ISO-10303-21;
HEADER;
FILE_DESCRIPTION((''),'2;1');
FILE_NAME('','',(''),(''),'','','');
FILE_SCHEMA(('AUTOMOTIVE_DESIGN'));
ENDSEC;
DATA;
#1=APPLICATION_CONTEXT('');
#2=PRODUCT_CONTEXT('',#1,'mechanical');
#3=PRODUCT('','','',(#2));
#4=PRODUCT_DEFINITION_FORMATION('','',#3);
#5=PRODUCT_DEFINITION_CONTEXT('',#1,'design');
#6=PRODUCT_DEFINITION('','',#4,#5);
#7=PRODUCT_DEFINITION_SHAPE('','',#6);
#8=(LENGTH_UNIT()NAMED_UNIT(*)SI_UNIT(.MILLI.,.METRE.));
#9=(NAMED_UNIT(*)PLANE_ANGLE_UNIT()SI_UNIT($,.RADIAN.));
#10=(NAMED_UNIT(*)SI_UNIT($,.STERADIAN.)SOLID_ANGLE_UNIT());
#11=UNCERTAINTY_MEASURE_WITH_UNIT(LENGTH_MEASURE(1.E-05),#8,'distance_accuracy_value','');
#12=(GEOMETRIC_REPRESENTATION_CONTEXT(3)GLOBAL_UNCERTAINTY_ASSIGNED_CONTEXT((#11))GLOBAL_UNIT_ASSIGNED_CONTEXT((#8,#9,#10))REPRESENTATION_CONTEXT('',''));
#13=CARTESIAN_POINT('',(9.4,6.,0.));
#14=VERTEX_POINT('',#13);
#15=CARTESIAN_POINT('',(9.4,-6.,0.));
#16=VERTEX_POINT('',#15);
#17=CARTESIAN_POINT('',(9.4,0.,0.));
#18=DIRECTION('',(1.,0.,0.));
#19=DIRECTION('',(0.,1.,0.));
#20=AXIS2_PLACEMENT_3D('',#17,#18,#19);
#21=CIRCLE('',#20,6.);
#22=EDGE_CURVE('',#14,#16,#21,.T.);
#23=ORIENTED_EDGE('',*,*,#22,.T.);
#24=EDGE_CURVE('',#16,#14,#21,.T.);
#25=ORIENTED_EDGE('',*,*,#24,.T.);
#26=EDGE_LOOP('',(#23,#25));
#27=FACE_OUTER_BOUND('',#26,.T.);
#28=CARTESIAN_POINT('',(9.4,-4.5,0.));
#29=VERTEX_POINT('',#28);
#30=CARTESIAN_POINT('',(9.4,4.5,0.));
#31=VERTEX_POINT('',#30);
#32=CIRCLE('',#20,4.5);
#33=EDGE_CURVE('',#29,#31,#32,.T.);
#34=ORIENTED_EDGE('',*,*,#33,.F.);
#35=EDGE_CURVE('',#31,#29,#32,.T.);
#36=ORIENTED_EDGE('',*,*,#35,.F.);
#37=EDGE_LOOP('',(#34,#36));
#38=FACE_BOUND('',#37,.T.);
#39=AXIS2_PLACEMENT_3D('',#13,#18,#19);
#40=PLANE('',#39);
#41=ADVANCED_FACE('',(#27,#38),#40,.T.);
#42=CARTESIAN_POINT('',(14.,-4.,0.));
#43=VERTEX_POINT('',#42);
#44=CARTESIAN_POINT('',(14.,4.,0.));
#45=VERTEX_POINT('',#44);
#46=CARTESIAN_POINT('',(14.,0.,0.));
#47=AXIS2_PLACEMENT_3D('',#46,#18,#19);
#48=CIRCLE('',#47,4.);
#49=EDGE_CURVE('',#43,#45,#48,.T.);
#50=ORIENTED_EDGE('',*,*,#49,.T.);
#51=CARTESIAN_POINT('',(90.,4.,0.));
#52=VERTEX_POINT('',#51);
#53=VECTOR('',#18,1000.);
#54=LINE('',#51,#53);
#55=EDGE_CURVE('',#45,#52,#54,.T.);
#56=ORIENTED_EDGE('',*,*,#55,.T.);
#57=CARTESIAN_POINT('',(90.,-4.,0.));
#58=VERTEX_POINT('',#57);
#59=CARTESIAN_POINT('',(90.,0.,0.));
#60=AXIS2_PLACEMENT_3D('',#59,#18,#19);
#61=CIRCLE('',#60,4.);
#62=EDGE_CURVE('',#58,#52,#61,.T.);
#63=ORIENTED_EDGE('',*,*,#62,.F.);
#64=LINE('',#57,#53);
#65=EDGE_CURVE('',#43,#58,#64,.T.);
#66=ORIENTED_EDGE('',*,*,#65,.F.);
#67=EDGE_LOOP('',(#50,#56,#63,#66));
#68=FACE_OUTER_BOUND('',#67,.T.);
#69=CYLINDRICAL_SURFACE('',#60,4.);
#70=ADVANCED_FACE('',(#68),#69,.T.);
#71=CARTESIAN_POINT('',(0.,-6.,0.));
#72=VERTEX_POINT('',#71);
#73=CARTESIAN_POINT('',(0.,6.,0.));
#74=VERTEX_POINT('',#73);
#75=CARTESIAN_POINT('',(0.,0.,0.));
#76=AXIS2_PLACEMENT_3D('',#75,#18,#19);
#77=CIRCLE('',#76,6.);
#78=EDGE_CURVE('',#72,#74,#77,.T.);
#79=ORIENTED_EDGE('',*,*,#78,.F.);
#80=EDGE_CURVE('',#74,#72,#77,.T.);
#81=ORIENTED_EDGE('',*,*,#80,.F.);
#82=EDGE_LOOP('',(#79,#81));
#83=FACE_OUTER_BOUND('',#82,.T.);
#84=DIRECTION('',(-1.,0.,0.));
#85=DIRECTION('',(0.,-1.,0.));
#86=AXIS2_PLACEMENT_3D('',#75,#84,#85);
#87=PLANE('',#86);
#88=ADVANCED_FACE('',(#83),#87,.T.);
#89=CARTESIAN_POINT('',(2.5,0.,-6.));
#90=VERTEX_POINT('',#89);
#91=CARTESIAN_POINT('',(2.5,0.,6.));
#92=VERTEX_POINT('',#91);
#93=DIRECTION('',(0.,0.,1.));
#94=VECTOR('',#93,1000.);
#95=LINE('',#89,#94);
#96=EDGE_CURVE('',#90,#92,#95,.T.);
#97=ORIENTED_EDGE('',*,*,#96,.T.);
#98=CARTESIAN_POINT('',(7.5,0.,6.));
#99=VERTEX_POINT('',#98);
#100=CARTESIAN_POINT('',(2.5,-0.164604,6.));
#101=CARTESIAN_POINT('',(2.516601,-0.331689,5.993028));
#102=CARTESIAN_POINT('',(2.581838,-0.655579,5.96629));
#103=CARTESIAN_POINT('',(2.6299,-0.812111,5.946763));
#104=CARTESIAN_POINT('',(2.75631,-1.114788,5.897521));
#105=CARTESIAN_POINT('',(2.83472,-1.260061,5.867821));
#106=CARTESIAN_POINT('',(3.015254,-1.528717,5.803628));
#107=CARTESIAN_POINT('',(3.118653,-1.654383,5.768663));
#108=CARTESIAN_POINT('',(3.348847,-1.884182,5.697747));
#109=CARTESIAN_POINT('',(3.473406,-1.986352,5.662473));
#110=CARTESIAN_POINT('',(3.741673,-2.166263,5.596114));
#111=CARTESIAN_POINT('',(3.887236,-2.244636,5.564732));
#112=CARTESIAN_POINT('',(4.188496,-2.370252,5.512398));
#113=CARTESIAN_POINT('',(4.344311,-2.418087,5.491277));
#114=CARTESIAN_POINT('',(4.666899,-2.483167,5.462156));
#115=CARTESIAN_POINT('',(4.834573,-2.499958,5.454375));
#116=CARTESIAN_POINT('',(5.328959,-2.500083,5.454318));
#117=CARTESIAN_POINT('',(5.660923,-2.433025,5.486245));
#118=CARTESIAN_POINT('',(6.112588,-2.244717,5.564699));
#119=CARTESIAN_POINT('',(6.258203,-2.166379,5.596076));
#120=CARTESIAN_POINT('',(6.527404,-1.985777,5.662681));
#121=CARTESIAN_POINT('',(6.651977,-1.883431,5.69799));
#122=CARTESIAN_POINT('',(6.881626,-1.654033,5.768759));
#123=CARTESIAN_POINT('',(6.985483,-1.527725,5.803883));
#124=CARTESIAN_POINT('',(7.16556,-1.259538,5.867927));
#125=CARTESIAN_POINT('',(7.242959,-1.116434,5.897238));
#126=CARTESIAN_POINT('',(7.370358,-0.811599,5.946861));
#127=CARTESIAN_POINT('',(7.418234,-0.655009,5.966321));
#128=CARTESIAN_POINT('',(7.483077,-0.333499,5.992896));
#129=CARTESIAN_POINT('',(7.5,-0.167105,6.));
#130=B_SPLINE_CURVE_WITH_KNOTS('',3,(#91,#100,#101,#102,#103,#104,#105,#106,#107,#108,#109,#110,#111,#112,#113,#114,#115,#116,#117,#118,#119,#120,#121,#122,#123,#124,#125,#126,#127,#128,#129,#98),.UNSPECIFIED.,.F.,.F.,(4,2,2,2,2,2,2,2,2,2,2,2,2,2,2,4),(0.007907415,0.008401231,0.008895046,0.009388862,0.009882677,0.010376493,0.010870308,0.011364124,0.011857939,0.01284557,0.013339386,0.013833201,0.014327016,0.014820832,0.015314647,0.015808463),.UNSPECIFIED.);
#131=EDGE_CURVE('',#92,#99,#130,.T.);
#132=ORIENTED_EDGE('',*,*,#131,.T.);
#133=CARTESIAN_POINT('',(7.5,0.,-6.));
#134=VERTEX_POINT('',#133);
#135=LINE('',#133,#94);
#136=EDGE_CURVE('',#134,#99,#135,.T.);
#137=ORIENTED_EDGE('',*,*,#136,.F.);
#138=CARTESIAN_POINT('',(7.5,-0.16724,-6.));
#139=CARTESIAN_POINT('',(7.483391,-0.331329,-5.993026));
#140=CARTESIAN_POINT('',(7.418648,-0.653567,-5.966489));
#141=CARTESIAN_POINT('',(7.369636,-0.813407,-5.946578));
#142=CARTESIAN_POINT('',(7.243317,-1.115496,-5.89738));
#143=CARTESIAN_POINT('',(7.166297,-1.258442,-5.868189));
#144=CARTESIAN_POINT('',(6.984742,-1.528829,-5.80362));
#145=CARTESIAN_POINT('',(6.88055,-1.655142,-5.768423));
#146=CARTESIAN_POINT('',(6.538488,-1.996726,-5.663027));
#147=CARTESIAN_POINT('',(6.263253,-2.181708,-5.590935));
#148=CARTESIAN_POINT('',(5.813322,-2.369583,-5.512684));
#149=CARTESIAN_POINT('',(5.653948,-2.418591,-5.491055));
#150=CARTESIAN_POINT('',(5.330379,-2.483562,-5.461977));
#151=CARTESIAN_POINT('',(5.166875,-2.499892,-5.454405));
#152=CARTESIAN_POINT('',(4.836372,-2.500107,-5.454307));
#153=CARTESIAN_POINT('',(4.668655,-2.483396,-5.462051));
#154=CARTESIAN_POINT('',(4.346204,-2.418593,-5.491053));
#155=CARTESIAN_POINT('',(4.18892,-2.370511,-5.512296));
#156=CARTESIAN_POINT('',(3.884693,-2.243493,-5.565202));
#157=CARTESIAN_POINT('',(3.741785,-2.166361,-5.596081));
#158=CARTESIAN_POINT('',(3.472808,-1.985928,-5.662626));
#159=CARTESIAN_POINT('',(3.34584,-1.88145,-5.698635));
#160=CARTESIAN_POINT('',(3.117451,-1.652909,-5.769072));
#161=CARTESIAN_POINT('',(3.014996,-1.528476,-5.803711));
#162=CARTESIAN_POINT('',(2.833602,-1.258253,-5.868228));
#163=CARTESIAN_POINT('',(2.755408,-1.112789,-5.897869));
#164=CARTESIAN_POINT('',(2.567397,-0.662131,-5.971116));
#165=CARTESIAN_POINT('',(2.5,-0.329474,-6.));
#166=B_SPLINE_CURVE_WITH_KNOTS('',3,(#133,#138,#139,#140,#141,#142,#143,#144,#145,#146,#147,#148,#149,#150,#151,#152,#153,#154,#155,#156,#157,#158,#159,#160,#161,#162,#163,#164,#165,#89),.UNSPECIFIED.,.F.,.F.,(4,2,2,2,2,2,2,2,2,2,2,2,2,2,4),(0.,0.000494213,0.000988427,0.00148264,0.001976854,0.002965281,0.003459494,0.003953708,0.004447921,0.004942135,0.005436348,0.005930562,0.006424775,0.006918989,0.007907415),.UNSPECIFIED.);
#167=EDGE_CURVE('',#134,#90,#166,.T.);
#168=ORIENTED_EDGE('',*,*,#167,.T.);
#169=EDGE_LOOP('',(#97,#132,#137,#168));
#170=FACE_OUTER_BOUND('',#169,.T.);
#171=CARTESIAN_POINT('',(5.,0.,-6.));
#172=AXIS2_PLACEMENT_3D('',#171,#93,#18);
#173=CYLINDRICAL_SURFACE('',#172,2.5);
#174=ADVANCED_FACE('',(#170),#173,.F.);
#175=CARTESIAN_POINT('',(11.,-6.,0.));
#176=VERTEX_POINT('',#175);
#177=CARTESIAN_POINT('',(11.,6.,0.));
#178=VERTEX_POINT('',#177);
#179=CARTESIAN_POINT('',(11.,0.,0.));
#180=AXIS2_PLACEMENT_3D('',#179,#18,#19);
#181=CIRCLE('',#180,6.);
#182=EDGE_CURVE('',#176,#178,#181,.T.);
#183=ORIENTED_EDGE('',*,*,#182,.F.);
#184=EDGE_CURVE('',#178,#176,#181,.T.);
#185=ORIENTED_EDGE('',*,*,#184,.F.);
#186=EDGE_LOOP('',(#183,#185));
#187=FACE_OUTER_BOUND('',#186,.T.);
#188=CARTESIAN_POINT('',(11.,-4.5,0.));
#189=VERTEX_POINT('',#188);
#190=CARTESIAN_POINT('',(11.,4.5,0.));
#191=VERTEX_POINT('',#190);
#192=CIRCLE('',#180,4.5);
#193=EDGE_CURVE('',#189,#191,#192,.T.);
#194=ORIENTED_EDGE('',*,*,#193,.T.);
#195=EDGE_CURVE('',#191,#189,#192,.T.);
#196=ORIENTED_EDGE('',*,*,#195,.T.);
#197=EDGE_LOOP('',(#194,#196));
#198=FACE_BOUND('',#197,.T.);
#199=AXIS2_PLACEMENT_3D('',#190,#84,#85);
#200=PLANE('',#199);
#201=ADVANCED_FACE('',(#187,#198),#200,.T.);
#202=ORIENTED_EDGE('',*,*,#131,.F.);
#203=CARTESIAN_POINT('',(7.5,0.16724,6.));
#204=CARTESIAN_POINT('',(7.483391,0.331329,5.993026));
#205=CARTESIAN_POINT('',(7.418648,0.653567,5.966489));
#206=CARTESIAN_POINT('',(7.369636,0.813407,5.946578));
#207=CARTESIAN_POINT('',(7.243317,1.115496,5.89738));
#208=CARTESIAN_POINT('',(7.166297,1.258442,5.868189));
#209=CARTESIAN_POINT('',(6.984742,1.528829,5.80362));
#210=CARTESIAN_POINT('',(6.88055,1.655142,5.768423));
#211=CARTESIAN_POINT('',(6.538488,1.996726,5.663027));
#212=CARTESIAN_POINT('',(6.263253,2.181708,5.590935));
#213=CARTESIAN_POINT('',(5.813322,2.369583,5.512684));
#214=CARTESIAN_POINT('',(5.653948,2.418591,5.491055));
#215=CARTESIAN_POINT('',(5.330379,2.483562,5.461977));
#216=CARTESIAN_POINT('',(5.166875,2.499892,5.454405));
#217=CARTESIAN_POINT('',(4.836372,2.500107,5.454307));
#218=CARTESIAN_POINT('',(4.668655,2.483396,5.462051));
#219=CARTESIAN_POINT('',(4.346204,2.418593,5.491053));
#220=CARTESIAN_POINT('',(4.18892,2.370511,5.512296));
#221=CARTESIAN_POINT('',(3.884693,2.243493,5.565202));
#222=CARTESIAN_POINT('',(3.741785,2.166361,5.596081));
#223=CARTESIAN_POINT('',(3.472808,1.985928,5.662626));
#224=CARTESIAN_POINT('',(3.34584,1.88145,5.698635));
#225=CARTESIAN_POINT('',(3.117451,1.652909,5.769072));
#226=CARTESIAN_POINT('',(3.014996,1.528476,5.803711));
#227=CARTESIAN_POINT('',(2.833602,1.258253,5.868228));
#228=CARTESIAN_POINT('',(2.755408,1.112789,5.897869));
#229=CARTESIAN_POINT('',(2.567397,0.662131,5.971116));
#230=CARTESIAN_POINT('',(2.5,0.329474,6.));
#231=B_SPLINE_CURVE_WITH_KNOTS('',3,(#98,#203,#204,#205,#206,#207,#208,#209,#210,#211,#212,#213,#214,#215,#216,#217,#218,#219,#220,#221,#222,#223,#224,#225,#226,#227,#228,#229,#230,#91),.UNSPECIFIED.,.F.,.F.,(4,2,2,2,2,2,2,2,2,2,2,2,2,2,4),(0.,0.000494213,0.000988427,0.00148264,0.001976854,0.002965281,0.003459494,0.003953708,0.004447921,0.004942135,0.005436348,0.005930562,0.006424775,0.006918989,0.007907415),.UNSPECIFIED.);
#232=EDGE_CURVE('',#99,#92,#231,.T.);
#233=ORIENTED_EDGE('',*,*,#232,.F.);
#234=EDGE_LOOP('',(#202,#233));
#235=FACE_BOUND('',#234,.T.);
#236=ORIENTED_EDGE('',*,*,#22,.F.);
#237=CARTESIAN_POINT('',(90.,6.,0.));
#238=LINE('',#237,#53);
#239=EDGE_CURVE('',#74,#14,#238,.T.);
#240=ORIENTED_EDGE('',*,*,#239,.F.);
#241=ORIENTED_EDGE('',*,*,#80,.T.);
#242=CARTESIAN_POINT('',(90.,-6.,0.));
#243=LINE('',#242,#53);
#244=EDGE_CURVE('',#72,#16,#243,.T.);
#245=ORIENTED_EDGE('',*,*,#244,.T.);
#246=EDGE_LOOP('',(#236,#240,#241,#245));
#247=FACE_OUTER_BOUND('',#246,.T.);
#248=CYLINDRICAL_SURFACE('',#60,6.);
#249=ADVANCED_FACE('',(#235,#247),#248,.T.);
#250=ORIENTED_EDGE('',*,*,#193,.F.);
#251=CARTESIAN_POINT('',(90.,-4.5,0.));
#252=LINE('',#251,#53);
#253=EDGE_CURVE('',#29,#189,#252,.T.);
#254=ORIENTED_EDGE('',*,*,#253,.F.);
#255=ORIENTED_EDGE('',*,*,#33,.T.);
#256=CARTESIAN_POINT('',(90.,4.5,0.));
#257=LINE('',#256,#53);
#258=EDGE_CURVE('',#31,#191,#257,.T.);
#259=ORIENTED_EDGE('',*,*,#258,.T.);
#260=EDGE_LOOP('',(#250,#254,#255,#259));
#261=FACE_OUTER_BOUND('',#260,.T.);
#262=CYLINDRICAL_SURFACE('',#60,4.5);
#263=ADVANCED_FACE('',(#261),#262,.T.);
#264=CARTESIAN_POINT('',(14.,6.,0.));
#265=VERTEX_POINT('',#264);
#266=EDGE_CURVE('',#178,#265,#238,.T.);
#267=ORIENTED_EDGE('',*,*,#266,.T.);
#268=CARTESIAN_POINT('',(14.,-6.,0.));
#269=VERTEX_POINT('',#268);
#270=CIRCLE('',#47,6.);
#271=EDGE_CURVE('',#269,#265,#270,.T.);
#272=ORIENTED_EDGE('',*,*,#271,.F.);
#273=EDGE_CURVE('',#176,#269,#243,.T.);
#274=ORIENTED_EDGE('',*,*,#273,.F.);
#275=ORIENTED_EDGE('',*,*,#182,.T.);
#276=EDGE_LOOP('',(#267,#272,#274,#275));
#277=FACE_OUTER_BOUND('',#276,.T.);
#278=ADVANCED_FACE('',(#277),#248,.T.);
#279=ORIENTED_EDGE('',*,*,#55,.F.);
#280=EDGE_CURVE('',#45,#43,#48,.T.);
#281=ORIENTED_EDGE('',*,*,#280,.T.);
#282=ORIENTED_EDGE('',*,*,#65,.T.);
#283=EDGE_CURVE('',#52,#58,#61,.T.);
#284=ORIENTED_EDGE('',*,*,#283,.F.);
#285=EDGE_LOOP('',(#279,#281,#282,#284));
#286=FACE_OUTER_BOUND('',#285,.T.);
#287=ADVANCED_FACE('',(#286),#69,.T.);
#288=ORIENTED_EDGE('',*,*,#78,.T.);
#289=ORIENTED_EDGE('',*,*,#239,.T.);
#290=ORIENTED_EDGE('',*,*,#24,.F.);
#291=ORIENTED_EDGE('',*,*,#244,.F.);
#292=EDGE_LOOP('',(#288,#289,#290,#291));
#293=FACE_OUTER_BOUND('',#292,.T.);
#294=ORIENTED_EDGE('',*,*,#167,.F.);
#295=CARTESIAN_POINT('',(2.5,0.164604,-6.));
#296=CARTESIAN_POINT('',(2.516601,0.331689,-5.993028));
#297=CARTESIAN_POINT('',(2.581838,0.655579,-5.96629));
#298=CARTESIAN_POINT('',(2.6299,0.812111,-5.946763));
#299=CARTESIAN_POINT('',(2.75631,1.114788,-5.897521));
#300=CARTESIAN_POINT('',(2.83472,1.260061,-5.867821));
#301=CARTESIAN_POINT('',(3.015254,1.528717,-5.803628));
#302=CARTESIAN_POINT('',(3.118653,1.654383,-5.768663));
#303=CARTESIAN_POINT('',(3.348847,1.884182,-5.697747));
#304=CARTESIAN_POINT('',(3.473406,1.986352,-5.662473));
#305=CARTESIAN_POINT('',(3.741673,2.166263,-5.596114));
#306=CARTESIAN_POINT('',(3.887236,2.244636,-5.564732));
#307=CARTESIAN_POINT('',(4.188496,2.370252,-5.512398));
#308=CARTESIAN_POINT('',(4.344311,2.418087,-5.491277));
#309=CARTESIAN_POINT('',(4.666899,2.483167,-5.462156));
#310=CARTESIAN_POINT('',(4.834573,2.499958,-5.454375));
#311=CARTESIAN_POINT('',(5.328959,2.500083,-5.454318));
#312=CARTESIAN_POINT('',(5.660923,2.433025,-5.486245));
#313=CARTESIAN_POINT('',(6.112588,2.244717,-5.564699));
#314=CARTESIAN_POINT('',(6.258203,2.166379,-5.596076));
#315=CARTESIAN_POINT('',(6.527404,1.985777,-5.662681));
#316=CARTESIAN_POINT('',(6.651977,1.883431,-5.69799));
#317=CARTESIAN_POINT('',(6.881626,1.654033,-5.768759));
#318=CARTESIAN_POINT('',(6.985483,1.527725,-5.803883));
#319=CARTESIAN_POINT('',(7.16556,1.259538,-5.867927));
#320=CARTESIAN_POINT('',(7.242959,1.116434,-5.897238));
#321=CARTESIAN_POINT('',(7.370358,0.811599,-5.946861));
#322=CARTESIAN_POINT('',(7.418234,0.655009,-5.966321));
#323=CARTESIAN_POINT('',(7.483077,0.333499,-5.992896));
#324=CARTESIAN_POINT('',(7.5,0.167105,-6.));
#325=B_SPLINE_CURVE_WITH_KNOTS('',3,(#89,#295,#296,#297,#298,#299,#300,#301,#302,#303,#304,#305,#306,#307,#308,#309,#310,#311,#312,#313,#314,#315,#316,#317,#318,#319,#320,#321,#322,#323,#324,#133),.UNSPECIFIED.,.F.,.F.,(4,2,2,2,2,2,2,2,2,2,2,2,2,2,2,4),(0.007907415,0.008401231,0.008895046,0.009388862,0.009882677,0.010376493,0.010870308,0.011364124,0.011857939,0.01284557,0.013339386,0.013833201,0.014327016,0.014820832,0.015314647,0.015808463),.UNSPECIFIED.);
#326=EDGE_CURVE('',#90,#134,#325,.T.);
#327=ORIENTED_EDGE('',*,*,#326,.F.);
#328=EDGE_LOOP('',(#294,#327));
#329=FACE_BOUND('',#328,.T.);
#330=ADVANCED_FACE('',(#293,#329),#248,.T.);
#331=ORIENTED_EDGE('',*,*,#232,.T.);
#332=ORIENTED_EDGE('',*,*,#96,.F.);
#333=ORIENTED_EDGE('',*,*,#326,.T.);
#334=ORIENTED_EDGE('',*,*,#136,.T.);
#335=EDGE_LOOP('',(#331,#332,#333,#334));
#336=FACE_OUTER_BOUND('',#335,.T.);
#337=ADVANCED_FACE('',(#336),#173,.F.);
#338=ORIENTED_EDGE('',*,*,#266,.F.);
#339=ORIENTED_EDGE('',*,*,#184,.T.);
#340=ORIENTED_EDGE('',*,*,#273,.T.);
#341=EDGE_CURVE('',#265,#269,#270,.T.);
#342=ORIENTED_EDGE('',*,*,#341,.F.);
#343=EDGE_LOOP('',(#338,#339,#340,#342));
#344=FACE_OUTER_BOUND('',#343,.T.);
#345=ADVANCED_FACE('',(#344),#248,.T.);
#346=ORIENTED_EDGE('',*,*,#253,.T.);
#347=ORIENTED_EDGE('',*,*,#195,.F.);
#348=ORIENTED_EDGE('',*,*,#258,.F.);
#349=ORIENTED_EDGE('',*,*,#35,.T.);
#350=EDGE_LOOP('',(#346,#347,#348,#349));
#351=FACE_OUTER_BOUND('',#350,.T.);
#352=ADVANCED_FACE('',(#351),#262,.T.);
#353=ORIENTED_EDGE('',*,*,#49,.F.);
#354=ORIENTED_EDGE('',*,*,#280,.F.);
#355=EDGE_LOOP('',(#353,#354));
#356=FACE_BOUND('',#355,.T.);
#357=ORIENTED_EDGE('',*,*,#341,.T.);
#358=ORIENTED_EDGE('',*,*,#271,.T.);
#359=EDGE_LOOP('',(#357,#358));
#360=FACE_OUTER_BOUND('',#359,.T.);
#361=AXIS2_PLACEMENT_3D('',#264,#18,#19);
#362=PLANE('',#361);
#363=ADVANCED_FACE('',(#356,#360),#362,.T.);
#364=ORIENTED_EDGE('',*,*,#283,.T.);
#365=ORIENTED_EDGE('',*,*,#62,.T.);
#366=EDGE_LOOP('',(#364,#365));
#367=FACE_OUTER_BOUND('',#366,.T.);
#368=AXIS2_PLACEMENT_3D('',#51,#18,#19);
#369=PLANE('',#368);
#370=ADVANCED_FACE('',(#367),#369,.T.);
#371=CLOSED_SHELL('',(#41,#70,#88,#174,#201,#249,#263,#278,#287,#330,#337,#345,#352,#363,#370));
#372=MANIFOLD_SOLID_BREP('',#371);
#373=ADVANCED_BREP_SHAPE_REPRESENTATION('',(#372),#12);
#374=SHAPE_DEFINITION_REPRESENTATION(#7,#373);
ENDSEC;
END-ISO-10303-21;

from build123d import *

# Parameters (mm, degrees)
CROSS_HOLE_DEPTH      = 91.39911504
CROSS_HOLE_DEPTH_BACK = 91.39911504
CROSS_HOLE_SKETCH_R   = 2.5


with BuildPart() as part:
    # Screw Profile Sketch → Screw Body Revolve (revolve)
    with BuildSketch(Plane.XY):
        Polygon((0, 0), (0, 6), (9.4, 6), (9.4, 4.5), (11, 4.5), (11, 6), (14, 6), (14, 4), (90, 4), (90, 0), align=None)
    revolve(axis=Axis((90, 0, 0), (-1, 0, 0)))

    # Cross Hole Sketch → Cross Hole (cut, two sides: drawn at the far end of the back side and taken through both)
    with BuildSketch(Plane.XY.offset(-CROSS_HOLE_DEPTH_BACK)):
        with Locations((5, 0)):
            Circle(CROSS_HOLE_SKETCH_R)
    extrude(amount=CROSS_HOLE_DEPTH + CROSS_HOLE_DEPTH_BACK, mode=Mode.SUBTRACT)


solid = part.part
